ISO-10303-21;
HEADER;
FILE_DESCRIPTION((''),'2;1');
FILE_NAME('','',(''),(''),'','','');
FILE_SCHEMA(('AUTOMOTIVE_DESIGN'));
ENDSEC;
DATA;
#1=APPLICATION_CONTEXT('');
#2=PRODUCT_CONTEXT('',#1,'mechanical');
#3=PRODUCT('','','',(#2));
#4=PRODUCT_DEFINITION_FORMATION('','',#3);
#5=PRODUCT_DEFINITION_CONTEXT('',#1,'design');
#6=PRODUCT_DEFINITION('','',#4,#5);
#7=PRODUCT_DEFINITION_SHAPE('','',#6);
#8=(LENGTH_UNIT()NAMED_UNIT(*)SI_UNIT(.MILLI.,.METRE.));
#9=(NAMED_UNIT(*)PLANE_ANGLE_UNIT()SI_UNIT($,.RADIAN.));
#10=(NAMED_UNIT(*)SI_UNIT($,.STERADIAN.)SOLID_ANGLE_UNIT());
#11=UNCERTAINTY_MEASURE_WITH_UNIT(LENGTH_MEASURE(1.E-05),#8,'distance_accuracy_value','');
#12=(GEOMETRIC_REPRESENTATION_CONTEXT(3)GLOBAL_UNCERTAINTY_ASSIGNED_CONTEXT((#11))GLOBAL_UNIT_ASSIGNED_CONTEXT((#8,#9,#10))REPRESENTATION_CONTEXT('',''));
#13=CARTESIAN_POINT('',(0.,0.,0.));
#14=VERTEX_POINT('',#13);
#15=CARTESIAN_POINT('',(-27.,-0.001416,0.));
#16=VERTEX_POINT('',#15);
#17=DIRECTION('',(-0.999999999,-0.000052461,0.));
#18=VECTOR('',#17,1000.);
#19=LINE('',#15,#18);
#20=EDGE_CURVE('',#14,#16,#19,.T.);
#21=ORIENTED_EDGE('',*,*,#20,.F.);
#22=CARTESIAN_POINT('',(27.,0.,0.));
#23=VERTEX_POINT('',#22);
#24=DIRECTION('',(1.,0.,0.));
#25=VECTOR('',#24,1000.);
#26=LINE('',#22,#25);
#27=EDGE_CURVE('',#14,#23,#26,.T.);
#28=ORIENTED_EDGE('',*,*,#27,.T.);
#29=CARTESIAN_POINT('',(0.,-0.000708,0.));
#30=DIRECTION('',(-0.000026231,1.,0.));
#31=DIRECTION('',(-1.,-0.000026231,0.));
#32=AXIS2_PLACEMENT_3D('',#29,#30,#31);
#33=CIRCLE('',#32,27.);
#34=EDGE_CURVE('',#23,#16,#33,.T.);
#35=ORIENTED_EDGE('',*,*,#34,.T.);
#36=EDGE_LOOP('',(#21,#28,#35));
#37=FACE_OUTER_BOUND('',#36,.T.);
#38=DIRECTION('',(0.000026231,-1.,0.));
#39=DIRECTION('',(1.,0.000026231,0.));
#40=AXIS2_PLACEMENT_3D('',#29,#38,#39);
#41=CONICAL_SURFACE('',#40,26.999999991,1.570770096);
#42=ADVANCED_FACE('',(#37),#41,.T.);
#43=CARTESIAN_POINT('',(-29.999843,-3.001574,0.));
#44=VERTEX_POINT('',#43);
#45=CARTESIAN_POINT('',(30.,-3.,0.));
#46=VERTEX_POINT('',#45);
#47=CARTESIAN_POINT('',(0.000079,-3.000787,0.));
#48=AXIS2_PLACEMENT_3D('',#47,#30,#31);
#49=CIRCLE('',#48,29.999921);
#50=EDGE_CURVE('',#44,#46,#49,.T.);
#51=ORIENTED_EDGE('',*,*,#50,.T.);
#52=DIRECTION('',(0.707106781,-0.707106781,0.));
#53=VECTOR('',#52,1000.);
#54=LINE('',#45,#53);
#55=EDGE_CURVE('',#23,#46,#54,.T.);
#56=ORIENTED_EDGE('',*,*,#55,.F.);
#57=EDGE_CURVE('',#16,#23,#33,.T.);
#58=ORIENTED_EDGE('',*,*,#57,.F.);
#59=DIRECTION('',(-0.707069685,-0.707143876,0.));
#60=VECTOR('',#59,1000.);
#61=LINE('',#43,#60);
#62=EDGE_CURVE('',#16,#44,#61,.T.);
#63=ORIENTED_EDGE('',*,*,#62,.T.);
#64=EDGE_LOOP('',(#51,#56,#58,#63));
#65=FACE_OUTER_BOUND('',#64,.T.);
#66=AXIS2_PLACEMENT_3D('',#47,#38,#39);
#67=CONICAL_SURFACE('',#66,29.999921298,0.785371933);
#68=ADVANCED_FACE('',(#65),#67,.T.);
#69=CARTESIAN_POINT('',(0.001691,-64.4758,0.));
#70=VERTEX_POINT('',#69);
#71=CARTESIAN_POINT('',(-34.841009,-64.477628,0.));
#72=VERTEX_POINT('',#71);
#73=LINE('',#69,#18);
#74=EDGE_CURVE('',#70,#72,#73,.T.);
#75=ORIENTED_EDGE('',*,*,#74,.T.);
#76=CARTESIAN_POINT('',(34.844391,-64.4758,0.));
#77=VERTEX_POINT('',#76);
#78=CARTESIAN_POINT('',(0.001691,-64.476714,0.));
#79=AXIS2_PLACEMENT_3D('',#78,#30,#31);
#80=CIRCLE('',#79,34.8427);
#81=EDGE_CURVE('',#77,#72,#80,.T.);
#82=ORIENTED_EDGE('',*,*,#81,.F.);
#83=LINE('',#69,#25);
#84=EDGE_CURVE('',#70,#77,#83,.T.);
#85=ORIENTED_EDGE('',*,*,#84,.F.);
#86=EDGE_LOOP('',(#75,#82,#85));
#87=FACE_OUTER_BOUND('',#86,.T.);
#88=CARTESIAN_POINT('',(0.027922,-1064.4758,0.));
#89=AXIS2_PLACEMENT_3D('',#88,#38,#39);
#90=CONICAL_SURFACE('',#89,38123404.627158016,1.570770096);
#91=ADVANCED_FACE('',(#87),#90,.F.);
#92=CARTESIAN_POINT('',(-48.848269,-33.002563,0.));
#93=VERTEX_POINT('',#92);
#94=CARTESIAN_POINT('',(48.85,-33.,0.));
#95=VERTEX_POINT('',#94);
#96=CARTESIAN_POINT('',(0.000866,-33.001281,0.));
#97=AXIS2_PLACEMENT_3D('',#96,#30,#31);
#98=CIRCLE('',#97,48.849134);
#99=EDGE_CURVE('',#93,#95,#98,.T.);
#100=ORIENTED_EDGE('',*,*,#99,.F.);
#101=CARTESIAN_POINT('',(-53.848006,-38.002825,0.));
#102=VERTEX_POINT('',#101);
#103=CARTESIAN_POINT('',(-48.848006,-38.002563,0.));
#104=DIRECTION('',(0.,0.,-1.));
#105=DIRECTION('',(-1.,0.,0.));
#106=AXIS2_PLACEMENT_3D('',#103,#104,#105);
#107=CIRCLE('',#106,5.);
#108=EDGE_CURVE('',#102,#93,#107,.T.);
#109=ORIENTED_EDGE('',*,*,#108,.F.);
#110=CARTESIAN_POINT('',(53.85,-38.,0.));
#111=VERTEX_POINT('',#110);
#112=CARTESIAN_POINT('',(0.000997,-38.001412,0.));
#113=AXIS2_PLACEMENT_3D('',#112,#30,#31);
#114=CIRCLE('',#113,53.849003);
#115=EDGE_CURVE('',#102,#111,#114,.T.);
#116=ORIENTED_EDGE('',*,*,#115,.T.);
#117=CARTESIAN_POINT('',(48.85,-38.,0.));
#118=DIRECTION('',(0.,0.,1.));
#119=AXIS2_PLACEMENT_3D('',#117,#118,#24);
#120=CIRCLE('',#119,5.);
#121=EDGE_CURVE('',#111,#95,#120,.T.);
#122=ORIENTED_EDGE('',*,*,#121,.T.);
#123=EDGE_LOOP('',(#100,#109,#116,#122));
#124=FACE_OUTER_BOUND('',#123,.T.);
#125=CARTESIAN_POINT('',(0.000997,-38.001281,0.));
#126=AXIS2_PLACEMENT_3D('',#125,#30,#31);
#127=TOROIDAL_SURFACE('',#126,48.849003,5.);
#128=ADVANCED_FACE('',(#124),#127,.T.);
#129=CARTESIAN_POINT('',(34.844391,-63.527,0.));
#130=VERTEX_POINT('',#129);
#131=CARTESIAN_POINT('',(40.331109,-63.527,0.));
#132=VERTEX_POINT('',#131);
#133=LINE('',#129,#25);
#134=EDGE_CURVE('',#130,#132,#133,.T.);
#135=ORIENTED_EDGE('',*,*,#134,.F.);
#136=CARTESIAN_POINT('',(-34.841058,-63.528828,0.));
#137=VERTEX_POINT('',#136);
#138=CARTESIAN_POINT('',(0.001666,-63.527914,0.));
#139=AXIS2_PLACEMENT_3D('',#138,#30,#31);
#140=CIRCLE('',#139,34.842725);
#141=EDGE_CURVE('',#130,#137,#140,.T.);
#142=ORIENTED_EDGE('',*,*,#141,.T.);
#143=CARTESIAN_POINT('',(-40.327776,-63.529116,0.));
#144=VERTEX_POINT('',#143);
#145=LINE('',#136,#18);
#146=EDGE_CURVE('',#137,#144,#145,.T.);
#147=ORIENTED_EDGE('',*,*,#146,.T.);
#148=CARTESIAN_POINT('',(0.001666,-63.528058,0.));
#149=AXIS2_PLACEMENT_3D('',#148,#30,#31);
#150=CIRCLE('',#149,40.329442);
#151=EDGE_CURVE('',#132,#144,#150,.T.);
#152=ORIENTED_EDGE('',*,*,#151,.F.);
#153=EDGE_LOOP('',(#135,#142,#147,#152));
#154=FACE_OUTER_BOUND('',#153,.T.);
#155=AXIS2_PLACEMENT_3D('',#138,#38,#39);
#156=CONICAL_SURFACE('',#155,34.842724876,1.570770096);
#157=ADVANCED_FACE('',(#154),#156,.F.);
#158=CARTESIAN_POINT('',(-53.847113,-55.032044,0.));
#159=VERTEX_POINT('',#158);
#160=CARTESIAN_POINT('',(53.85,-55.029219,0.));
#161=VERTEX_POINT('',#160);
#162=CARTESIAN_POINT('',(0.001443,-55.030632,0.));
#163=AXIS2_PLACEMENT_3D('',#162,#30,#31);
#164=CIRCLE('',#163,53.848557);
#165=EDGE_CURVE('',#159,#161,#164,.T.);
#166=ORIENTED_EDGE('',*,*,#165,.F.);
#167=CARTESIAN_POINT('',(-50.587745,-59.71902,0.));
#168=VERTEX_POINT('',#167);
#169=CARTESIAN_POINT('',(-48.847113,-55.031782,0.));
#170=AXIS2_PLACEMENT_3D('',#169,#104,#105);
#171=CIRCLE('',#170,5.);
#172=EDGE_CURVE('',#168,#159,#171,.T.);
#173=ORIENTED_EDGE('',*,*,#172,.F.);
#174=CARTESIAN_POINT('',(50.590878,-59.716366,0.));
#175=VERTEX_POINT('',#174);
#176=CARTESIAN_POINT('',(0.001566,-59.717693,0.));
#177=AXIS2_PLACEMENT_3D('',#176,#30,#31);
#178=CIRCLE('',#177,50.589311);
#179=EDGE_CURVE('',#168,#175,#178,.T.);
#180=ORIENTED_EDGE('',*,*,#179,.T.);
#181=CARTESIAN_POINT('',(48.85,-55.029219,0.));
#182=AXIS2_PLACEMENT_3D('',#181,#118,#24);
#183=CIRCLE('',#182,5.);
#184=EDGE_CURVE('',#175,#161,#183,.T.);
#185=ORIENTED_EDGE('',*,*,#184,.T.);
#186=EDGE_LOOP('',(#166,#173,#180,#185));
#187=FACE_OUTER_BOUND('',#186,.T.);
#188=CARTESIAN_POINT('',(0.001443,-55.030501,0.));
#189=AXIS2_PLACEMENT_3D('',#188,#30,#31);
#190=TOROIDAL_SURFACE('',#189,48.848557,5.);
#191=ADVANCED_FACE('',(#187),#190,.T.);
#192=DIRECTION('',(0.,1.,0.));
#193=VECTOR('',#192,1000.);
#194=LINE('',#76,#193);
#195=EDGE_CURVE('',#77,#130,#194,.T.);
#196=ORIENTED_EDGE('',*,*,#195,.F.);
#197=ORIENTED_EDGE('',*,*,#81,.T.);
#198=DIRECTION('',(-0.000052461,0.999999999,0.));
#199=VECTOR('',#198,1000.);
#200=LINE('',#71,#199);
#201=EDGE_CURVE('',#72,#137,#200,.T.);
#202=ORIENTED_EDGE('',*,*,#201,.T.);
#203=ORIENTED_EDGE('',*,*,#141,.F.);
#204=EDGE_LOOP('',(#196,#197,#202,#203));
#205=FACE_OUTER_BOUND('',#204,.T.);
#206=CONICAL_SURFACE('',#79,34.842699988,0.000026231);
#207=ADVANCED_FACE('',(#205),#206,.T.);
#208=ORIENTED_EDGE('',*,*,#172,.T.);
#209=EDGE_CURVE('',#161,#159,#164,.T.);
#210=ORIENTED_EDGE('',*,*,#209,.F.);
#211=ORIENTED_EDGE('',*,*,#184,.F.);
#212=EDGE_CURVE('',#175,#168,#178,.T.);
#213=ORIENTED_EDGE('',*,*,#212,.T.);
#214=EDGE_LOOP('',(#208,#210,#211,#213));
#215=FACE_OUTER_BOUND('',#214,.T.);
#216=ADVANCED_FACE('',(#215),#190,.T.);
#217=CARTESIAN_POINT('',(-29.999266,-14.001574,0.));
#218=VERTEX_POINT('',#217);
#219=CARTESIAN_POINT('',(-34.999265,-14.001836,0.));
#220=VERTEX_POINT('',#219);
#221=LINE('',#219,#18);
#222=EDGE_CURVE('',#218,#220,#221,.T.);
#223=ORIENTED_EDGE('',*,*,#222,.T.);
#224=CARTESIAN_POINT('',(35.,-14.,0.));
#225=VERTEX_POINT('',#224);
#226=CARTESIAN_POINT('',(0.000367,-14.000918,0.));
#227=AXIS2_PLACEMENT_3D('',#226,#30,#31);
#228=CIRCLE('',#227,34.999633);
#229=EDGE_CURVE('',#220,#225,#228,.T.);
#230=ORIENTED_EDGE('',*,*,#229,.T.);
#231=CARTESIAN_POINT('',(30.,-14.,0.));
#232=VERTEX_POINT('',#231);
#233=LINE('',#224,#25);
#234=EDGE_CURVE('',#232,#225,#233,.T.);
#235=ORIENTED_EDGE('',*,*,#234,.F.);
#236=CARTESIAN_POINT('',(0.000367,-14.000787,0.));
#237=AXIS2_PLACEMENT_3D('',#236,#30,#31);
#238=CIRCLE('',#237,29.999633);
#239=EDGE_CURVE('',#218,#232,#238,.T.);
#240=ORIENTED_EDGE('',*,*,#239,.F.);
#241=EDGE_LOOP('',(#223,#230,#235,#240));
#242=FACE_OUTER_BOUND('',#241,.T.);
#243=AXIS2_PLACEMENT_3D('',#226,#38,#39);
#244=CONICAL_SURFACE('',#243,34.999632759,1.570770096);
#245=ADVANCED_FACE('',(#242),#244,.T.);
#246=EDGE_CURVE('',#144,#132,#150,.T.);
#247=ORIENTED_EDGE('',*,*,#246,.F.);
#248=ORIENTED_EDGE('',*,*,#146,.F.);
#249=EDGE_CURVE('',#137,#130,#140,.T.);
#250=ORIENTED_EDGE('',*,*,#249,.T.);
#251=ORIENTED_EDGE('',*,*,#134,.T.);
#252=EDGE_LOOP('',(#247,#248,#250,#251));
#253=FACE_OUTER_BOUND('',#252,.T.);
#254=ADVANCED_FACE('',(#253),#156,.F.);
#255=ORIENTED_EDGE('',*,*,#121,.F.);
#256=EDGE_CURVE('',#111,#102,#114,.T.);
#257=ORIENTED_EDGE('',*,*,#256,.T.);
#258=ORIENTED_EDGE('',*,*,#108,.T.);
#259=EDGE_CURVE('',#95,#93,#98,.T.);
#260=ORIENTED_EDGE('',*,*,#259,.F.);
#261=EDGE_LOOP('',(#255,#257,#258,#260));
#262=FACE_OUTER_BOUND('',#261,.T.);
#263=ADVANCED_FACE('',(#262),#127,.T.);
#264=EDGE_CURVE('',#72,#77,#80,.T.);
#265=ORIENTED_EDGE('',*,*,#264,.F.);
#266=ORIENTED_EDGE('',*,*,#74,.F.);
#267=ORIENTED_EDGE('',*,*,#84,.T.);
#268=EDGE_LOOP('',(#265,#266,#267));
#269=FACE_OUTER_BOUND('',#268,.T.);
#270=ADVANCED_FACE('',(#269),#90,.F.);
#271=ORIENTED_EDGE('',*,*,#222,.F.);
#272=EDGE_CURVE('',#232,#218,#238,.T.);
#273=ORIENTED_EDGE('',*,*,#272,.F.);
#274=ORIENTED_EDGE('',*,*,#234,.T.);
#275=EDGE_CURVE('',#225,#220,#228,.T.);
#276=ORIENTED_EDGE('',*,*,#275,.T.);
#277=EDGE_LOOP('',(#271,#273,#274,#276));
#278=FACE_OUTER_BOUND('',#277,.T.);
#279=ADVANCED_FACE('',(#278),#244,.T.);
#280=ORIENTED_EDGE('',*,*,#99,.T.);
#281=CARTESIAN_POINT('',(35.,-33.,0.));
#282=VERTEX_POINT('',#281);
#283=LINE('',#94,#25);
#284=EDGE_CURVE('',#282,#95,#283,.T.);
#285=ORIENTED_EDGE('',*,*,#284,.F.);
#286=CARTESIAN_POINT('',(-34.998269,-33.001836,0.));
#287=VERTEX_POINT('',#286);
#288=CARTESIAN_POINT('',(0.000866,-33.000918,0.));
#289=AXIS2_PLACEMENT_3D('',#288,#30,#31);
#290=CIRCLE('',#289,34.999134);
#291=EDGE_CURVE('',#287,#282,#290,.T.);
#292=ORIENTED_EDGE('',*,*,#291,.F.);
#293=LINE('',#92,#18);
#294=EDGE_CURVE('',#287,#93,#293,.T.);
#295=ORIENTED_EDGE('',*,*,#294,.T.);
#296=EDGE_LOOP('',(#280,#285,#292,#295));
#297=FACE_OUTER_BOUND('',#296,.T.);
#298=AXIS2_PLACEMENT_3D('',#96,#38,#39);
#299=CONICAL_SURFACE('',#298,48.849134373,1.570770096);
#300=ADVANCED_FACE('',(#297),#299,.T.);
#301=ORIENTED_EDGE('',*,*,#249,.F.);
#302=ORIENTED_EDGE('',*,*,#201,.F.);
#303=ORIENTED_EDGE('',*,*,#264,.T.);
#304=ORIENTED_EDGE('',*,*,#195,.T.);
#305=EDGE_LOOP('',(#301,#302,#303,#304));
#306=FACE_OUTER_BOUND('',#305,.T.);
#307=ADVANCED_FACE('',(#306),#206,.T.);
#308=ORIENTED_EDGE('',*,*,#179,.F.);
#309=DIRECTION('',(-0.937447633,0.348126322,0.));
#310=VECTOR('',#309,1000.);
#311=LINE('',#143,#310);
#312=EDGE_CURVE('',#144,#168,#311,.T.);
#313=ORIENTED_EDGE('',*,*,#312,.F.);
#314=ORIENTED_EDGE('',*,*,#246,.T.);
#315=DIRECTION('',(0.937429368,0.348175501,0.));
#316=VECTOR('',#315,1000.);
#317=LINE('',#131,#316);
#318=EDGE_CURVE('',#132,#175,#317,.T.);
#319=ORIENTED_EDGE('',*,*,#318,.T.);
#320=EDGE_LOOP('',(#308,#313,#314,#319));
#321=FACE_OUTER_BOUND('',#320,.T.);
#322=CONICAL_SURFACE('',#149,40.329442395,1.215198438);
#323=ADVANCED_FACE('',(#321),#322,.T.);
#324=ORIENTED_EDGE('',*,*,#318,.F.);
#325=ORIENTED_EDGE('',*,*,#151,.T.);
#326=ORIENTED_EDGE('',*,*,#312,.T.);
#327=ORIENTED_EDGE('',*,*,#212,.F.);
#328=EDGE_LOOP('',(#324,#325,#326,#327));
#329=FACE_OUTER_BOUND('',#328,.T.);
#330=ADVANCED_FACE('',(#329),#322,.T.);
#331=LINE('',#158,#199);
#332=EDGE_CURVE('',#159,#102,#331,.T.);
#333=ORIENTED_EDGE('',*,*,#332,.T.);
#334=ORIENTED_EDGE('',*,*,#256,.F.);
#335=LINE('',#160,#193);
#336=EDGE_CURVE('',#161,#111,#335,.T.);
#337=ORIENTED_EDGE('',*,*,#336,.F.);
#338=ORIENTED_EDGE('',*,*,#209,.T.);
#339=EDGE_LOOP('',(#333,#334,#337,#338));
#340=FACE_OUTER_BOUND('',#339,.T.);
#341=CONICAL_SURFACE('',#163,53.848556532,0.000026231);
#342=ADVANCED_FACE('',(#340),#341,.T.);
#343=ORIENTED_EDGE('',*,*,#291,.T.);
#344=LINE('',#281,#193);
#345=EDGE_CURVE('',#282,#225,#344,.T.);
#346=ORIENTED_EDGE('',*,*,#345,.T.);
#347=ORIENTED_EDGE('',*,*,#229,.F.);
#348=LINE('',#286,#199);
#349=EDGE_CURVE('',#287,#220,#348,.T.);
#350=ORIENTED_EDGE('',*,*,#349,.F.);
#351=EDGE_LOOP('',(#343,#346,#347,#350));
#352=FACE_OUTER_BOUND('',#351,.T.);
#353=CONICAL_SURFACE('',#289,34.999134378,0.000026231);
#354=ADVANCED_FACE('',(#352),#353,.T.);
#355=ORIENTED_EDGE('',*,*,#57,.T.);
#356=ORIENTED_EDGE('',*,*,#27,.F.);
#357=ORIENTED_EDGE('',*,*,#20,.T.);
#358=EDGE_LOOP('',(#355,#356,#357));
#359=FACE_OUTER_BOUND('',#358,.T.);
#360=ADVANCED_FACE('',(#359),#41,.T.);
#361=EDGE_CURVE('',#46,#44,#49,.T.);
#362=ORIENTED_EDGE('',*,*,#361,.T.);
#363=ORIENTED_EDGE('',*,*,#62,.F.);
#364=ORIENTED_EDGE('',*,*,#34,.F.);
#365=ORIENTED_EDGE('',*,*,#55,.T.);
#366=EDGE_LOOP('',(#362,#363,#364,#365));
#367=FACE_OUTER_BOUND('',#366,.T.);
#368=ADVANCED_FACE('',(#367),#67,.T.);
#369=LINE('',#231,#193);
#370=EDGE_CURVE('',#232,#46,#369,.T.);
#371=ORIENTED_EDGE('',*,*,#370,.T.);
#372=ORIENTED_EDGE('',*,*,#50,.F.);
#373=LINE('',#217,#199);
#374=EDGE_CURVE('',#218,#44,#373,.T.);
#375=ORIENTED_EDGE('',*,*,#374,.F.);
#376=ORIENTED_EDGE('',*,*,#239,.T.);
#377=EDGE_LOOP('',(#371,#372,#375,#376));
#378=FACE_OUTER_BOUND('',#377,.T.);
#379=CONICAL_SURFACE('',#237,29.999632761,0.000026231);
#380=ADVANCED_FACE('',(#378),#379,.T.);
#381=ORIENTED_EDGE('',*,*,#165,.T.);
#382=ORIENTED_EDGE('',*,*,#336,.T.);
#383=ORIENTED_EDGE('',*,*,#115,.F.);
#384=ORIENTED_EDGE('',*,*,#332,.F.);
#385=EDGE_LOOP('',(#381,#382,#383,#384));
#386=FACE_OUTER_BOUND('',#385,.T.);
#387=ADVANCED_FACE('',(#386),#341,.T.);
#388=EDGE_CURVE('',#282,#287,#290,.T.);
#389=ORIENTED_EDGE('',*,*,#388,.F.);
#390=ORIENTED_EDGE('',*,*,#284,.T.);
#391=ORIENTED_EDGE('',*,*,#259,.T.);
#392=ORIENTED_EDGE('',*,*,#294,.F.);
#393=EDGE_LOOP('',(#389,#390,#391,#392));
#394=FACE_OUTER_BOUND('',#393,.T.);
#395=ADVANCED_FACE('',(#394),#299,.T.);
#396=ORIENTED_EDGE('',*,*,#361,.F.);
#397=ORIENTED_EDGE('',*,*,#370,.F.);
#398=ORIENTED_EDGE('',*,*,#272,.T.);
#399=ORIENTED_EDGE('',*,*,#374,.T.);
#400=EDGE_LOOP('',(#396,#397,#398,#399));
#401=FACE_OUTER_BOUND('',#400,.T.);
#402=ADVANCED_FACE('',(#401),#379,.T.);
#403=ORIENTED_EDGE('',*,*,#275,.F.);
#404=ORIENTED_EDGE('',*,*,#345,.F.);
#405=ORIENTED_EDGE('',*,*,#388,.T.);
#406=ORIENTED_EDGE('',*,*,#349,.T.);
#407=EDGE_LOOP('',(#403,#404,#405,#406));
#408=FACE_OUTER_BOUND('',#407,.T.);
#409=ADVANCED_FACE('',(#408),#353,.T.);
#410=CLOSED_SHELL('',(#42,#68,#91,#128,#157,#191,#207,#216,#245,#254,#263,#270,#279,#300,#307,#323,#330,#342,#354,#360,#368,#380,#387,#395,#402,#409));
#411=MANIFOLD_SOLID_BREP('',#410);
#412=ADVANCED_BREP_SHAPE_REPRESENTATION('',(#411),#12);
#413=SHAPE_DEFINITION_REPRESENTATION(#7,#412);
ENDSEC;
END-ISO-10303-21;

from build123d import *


with BuildPart() as part:
    # Sketch1 → Revolve1 (revolve)
    with BuildSketch(Plane.XY, mode=Mode.PRIVATE) as revolve1_sk:
        with BuildLine():
            Line((0, 0), (27, 0))
            Line((27, 0), (30, -3))
            Line((30, -3), (30, -14))
            Line((30, -14), (35, -14))
            Line((35, -14), (35, -33))
            Line((35, -33), (48.85, -33))
            ThreePointArc((48.85, -33), (52.385533906, -34.464466094), (53.85, -38))
            Line((53.85, -38), (53.85, -55.029219265))
            ThreePointArc((53.85, -55.029219265), (52.955142356, -57.883655503), (50.590877505, -59.716366106))
            Line((50.590877505, -59.716366106), (40.331108761, -63.527))
            Line((40.331108761, -63.527), (34.844391239, -63.527))
            Line((34.844391239, -63.527), (34.844391239, -64.4758))
            Line((34.844391239, -64.4758), (0.001691239, -64.4758))
            Line((0.001691239, -64.4758), (0, 0))
        make_face()
    revolve(revolve1_sk.sketch.rotate(Axis((0, 0, 0), (2.6230605830006534e-05, -0.9999999996559776, 0)), 180), axis=Axis((0, 0, 0), (2.6230605830006534e-05, -0.9999999996559776, 0)))


solid = part.part
